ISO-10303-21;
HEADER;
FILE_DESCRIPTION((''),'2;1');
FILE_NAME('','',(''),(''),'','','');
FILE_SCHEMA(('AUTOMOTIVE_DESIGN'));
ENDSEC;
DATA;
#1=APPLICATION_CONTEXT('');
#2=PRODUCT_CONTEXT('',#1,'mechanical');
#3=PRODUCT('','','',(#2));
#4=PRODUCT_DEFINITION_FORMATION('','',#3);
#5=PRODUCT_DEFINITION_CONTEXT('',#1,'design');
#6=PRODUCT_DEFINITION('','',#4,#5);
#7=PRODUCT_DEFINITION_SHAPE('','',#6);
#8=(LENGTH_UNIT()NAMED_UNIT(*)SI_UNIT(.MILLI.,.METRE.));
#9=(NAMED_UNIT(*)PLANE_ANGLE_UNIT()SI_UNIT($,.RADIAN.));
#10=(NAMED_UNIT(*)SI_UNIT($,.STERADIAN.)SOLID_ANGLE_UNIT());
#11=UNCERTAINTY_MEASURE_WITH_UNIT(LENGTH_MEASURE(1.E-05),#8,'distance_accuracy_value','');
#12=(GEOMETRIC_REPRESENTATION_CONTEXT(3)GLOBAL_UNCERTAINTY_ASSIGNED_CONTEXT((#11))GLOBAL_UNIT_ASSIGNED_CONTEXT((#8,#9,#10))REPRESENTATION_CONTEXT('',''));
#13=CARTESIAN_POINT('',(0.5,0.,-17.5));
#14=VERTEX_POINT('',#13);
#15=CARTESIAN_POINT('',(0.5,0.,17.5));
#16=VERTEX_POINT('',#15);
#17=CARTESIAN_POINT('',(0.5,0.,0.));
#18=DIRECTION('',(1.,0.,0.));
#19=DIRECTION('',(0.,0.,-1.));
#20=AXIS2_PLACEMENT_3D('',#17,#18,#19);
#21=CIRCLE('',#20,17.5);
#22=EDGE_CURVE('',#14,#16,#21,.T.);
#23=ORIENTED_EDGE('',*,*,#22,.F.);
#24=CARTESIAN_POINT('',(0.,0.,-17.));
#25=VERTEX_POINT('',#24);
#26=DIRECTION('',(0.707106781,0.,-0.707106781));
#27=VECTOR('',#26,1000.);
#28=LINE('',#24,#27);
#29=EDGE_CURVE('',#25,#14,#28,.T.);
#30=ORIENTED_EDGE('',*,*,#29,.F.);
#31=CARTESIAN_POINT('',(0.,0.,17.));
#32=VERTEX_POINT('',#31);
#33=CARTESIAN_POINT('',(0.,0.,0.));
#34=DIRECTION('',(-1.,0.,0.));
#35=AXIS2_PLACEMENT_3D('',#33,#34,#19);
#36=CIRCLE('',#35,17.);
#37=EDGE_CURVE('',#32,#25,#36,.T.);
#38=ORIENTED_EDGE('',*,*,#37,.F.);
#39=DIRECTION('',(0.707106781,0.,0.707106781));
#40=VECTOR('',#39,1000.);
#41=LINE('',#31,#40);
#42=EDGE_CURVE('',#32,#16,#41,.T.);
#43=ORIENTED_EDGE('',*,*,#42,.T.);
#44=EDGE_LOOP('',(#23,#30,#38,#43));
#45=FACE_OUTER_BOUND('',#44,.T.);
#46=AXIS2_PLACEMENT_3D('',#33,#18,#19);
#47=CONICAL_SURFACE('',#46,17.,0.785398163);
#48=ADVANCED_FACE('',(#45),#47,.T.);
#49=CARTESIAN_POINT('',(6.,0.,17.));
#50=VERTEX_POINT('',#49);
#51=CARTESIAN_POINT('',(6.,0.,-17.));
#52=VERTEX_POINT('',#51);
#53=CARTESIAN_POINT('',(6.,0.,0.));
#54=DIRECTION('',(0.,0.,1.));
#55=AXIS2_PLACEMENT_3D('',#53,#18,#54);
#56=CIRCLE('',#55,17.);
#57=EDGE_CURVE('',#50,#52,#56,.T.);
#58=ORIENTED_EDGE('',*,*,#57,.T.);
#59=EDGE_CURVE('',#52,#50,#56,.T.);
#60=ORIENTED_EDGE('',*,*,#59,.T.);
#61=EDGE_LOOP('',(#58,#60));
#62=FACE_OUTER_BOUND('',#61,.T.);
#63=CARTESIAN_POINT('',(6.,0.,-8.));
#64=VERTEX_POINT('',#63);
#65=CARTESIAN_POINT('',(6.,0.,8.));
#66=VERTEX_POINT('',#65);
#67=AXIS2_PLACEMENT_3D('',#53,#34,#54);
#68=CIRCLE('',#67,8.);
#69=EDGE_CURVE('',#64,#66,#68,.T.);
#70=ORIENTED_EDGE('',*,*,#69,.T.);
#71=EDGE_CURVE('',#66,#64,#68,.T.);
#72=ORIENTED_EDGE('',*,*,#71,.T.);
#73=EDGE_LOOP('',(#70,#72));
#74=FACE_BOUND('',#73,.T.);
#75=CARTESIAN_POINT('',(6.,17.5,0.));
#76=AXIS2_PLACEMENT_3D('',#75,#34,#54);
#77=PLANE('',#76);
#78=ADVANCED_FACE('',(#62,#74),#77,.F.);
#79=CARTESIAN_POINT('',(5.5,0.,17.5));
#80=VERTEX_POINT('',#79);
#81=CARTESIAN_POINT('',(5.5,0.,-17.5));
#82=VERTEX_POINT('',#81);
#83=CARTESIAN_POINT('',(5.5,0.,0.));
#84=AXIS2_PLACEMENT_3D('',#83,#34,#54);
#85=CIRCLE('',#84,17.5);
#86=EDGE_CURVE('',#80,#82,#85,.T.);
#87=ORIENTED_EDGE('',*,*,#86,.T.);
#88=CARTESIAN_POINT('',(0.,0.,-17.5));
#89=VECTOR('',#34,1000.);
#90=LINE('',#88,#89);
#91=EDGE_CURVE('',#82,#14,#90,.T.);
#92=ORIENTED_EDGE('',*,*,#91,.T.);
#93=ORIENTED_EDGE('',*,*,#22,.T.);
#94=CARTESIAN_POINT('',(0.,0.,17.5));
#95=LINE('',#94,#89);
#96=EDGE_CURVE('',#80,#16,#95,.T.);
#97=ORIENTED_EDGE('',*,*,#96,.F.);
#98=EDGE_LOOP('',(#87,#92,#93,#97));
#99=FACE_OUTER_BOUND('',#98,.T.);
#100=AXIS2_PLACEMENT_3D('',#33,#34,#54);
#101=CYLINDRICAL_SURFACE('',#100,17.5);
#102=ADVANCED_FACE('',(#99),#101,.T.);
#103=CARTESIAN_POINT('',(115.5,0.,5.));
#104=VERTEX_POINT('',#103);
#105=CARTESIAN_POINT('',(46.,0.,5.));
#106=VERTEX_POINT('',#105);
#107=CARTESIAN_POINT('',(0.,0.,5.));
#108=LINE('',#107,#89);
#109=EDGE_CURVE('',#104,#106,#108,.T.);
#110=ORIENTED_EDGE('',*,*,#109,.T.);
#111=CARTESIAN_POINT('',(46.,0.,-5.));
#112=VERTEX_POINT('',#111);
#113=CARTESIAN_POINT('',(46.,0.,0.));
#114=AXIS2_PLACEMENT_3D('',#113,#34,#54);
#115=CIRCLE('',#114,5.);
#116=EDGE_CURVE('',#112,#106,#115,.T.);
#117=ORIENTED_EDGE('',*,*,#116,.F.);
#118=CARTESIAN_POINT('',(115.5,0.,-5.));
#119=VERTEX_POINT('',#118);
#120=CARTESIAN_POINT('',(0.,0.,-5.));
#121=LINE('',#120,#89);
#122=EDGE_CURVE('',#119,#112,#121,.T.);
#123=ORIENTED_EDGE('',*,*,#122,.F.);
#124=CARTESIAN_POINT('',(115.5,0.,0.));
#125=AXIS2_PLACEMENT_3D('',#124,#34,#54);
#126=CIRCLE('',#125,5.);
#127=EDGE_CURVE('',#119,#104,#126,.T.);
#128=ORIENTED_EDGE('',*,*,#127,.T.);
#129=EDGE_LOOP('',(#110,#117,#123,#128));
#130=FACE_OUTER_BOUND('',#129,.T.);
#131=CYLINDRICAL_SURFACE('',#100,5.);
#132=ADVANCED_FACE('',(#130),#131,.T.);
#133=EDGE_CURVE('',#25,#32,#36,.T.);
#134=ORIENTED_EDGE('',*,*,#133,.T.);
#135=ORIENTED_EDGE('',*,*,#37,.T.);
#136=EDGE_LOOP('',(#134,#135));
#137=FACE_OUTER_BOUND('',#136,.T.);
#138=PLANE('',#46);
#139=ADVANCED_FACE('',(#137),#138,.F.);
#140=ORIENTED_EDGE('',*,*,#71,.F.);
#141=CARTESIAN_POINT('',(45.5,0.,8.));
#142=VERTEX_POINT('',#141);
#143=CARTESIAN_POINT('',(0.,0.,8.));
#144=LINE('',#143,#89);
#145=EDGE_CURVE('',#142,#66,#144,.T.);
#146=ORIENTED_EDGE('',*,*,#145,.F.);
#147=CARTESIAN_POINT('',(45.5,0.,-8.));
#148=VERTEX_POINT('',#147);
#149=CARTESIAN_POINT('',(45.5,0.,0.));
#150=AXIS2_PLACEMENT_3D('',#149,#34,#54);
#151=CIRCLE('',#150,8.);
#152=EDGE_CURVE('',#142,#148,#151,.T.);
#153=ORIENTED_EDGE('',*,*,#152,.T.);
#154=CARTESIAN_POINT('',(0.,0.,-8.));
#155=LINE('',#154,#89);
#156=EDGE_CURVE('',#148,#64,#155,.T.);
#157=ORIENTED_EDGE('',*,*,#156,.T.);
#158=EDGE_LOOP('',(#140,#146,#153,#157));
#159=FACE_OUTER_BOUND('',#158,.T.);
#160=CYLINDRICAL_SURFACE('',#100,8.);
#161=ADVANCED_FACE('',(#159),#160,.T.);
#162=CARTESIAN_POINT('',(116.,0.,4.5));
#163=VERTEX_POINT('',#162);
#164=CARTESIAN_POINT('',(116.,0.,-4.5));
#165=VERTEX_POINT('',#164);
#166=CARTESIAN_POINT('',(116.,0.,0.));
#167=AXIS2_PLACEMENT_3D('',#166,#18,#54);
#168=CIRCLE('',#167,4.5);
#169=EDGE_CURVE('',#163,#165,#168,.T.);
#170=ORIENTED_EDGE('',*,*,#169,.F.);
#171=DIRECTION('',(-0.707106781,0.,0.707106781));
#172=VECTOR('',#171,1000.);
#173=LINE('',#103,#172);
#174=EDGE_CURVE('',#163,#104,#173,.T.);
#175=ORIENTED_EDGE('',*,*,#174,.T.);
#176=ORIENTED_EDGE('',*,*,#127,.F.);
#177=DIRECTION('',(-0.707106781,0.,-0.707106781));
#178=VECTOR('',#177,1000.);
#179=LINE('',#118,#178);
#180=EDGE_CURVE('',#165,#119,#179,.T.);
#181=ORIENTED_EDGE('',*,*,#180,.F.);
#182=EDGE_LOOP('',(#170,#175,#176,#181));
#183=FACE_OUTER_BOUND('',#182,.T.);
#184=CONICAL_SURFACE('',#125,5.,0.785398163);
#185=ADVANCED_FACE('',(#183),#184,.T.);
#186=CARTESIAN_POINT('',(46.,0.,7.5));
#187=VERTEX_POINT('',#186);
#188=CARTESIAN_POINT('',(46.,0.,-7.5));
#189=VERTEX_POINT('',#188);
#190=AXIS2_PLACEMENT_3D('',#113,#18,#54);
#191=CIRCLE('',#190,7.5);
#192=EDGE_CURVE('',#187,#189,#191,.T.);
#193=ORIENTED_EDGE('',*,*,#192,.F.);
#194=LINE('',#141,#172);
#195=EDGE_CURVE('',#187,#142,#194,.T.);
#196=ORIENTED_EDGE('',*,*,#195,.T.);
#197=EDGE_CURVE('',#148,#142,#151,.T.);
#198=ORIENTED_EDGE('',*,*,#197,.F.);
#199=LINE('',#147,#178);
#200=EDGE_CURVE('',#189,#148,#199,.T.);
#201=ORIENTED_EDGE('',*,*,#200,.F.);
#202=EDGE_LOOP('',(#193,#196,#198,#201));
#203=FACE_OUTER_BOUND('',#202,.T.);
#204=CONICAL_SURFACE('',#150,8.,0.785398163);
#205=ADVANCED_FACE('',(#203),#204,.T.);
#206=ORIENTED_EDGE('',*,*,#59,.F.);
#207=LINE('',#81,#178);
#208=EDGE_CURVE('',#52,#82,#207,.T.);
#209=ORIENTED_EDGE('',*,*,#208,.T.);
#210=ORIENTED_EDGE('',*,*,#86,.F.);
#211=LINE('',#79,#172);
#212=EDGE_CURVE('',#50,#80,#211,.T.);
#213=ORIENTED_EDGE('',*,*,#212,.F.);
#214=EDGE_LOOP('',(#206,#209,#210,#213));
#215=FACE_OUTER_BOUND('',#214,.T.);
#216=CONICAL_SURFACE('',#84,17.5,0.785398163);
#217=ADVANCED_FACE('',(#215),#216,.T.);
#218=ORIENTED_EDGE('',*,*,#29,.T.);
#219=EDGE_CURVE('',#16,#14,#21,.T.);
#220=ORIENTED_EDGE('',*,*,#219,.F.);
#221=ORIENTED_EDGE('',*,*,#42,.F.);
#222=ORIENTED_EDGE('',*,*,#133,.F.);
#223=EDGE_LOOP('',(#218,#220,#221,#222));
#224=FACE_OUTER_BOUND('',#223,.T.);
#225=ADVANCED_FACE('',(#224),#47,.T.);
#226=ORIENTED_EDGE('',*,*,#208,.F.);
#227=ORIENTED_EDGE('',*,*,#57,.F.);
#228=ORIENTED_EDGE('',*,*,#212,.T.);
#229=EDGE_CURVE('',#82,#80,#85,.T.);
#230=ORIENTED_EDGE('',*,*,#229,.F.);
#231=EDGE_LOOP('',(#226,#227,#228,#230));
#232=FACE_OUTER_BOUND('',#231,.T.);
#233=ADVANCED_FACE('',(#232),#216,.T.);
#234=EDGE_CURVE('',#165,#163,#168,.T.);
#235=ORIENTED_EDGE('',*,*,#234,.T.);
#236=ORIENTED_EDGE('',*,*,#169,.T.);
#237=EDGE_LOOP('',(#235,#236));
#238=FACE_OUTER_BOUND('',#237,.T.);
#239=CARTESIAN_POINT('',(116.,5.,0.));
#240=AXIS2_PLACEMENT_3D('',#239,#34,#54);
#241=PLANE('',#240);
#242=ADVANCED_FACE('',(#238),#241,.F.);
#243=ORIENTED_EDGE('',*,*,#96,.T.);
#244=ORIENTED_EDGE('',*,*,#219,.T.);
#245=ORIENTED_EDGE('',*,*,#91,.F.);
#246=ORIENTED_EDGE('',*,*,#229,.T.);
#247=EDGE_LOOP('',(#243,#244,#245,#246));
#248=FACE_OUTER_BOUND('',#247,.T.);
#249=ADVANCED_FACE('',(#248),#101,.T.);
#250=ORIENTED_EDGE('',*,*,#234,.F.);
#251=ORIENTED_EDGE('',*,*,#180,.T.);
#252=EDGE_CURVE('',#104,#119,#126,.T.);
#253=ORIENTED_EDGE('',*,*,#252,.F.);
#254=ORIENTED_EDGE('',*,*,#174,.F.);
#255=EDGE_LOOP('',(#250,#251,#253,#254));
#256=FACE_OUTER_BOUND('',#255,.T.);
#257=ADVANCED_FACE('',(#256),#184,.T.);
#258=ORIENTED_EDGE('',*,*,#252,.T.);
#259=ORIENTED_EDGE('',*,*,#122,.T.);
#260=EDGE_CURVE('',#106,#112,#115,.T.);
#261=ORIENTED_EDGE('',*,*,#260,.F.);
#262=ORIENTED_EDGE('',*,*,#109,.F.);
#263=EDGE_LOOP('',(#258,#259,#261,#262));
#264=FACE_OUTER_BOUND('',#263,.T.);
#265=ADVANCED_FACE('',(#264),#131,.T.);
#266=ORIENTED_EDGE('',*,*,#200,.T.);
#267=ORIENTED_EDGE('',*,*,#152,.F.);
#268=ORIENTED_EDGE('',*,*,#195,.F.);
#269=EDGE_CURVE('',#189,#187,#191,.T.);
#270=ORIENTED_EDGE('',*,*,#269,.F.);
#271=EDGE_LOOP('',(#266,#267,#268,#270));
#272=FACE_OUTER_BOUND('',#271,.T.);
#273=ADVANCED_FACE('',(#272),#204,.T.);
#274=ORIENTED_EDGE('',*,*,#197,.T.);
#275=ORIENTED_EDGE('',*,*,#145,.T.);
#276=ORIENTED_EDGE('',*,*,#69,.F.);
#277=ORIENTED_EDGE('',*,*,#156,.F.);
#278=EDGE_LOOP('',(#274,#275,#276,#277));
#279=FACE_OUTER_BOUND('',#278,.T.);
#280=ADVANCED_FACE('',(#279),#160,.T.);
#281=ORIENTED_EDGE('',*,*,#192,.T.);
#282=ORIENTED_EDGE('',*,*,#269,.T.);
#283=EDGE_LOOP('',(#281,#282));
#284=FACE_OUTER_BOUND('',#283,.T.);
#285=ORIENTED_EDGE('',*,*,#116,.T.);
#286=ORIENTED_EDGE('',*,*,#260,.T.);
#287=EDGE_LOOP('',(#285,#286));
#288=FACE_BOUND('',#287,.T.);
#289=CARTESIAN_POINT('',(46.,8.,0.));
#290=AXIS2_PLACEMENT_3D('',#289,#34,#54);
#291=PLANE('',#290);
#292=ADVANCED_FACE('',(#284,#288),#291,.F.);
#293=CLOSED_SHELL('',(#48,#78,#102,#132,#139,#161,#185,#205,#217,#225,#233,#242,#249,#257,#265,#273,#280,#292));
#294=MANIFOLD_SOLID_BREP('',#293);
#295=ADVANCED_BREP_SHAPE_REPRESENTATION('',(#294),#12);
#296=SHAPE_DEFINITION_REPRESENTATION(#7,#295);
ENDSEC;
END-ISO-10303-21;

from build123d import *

# Parameters (mm, degrees)
CHAMFER1_SIZE = 0.5
CHAMFER2_SIZE = 0.5


with BuildPart() as part:
    # Sketch1 → Revolve1 (revolve)
    with BuildSketch(Plane.XY, mode=Mode.PRIVATE) as revolve1_sk:
        Polygon((0, 0), (0, 17.5), (6, 17.5), (6, 8), (46, 8), (46, 5), (116, 5), (116, 0), align=None)
    revolve(revolve1_sk.sketch.rotate(Axis((0, 0, 0), (1, 0, 0)), 90), axis=Axis((0, 0, 0), (1, 0, 0)))

    # Chamfer1
    chamfer1_edges = [part.edges().sort_by_distance(p)[0] for p in [
        (46, 0, -8),
        (6, 0, -17.5),
        (0, 0, -17.5),
    ]]
    chamfer(chamfer1_edges, length=CHAMFER1_SIZE)

    # Chamfer2
    chamfer2_edges = [part.edges().sort_by_distance(p)[0] for p in [
        (116, 0, -5),
    ]]
    chamfer(chamfer2_edges, length=CHAMFER2_SIZE)


solid = part.part
